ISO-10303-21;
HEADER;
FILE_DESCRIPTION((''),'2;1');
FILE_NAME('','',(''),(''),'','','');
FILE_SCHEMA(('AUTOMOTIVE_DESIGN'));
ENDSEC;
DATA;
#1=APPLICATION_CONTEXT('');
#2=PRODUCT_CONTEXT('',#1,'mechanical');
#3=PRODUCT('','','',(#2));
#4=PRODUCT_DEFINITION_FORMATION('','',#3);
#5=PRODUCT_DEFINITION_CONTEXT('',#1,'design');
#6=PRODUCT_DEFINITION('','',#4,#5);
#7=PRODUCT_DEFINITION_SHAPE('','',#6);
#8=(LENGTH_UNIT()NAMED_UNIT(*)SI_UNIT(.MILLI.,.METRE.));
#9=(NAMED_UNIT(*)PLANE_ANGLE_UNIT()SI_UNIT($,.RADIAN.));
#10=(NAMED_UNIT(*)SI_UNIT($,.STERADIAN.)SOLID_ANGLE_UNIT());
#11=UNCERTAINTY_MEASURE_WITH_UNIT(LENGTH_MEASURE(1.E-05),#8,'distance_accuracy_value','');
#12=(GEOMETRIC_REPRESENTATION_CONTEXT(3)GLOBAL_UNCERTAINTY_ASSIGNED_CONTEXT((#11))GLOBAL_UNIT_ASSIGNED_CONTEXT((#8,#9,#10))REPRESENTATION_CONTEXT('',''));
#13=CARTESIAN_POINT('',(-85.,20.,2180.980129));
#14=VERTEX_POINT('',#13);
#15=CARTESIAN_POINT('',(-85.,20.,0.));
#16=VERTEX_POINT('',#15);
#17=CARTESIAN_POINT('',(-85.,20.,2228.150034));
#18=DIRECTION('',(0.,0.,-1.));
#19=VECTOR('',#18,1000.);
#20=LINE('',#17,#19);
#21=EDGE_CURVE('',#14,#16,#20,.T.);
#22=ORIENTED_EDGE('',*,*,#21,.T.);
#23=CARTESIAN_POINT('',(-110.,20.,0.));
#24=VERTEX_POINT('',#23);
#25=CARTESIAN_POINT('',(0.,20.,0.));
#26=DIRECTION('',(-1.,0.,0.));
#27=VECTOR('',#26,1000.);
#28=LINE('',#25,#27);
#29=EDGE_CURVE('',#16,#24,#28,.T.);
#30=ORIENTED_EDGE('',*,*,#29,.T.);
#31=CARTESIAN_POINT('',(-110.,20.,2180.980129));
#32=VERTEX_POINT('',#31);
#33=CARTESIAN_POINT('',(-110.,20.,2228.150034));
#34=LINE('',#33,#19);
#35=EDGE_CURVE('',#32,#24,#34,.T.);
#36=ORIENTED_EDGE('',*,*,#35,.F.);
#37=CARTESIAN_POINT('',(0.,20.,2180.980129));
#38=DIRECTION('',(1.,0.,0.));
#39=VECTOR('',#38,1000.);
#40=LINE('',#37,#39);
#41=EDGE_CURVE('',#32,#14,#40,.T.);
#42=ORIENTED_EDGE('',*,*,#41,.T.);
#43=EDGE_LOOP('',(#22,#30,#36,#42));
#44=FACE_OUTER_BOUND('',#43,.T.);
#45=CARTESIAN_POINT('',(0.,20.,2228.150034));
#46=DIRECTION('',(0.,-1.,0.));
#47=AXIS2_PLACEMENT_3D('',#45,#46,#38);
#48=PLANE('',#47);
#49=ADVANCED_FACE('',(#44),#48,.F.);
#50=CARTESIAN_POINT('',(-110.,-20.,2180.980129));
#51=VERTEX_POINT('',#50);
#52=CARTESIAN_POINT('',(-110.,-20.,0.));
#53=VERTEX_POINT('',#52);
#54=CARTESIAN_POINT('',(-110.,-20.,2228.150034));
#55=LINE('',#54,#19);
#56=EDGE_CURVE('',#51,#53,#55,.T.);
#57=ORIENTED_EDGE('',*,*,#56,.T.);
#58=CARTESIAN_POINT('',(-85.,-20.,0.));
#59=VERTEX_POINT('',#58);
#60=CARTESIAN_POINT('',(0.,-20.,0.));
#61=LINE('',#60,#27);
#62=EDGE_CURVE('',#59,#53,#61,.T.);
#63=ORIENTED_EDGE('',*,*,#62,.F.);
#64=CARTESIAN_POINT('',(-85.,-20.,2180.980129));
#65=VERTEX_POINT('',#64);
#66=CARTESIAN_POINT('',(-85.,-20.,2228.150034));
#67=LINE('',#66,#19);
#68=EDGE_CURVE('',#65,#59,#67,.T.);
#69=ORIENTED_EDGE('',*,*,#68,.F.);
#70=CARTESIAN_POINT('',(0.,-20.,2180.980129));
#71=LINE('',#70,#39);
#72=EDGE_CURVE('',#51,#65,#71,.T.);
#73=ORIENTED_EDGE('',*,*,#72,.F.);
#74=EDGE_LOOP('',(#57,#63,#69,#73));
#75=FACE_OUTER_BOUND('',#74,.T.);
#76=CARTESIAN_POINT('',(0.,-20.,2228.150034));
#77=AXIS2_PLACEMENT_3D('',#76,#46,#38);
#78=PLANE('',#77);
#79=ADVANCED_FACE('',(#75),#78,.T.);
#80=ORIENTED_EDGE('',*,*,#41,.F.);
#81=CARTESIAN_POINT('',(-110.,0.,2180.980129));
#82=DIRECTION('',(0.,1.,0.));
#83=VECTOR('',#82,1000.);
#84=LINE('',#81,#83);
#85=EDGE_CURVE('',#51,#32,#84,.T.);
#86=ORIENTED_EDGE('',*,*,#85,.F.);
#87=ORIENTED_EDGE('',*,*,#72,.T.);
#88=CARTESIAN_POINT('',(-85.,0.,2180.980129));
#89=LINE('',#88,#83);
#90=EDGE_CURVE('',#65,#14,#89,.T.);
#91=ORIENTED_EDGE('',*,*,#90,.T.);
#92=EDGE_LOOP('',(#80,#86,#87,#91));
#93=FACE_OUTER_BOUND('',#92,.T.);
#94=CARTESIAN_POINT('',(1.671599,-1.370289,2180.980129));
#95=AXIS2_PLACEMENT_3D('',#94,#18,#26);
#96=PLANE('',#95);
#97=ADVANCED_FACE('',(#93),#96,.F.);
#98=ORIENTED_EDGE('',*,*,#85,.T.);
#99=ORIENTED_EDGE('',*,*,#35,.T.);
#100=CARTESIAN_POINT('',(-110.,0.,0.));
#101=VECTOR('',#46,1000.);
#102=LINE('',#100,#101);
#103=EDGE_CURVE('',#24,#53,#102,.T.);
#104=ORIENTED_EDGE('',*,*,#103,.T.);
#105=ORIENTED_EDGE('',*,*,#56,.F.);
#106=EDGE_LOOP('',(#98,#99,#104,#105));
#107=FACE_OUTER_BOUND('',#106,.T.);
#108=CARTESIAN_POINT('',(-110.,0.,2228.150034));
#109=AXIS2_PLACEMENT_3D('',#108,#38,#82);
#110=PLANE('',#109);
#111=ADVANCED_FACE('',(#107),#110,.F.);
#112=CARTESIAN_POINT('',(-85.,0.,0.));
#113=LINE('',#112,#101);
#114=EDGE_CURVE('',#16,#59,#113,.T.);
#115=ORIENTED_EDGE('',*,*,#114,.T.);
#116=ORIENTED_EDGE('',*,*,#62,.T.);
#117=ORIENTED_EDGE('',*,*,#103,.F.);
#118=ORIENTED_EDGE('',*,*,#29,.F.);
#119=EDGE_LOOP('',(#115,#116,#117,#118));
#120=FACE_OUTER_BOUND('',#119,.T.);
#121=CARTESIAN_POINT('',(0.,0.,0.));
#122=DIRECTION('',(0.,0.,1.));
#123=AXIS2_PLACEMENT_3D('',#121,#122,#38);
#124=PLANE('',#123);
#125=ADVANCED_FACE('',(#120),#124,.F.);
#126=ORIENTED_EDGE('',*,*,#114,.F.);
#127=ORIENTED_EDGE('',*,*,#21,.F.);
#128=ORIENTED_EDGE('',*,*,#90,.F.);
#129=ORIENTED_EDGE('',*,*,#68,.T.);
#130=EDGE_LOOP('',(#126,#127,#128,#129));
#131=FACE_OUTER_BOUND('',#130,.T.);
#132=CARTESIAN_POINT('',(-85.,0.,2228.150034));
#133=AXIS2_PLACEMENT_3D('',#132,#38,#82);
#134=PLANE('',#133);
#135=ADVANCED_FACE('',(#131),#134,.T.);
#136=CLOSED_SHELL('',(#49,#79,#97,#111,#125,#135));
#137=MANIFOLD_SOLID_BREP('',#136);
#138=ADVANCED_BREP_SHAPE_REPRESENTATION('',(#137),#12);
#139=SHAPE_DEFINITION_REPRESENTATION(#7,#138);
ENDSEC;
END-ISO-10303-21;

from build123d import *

# Parameters (mm, degrees)
SKETCH_1_W      = 25
SKETCH_1_H      = 40
EXTRUDE_1_DEPTH = 2180.980128516


with BuildPart() as part:
    # 草图1 → 凸台-拉伸1 (new body)
    with BuildSketch(Plane.XY):
        with Locations((-97.5, 0)):
            Rectangle(SKETCH_1_W, SKETCH_1_H)
    extrude(amount=EXTRUDE_1_DEPTH)


solid = part.part
